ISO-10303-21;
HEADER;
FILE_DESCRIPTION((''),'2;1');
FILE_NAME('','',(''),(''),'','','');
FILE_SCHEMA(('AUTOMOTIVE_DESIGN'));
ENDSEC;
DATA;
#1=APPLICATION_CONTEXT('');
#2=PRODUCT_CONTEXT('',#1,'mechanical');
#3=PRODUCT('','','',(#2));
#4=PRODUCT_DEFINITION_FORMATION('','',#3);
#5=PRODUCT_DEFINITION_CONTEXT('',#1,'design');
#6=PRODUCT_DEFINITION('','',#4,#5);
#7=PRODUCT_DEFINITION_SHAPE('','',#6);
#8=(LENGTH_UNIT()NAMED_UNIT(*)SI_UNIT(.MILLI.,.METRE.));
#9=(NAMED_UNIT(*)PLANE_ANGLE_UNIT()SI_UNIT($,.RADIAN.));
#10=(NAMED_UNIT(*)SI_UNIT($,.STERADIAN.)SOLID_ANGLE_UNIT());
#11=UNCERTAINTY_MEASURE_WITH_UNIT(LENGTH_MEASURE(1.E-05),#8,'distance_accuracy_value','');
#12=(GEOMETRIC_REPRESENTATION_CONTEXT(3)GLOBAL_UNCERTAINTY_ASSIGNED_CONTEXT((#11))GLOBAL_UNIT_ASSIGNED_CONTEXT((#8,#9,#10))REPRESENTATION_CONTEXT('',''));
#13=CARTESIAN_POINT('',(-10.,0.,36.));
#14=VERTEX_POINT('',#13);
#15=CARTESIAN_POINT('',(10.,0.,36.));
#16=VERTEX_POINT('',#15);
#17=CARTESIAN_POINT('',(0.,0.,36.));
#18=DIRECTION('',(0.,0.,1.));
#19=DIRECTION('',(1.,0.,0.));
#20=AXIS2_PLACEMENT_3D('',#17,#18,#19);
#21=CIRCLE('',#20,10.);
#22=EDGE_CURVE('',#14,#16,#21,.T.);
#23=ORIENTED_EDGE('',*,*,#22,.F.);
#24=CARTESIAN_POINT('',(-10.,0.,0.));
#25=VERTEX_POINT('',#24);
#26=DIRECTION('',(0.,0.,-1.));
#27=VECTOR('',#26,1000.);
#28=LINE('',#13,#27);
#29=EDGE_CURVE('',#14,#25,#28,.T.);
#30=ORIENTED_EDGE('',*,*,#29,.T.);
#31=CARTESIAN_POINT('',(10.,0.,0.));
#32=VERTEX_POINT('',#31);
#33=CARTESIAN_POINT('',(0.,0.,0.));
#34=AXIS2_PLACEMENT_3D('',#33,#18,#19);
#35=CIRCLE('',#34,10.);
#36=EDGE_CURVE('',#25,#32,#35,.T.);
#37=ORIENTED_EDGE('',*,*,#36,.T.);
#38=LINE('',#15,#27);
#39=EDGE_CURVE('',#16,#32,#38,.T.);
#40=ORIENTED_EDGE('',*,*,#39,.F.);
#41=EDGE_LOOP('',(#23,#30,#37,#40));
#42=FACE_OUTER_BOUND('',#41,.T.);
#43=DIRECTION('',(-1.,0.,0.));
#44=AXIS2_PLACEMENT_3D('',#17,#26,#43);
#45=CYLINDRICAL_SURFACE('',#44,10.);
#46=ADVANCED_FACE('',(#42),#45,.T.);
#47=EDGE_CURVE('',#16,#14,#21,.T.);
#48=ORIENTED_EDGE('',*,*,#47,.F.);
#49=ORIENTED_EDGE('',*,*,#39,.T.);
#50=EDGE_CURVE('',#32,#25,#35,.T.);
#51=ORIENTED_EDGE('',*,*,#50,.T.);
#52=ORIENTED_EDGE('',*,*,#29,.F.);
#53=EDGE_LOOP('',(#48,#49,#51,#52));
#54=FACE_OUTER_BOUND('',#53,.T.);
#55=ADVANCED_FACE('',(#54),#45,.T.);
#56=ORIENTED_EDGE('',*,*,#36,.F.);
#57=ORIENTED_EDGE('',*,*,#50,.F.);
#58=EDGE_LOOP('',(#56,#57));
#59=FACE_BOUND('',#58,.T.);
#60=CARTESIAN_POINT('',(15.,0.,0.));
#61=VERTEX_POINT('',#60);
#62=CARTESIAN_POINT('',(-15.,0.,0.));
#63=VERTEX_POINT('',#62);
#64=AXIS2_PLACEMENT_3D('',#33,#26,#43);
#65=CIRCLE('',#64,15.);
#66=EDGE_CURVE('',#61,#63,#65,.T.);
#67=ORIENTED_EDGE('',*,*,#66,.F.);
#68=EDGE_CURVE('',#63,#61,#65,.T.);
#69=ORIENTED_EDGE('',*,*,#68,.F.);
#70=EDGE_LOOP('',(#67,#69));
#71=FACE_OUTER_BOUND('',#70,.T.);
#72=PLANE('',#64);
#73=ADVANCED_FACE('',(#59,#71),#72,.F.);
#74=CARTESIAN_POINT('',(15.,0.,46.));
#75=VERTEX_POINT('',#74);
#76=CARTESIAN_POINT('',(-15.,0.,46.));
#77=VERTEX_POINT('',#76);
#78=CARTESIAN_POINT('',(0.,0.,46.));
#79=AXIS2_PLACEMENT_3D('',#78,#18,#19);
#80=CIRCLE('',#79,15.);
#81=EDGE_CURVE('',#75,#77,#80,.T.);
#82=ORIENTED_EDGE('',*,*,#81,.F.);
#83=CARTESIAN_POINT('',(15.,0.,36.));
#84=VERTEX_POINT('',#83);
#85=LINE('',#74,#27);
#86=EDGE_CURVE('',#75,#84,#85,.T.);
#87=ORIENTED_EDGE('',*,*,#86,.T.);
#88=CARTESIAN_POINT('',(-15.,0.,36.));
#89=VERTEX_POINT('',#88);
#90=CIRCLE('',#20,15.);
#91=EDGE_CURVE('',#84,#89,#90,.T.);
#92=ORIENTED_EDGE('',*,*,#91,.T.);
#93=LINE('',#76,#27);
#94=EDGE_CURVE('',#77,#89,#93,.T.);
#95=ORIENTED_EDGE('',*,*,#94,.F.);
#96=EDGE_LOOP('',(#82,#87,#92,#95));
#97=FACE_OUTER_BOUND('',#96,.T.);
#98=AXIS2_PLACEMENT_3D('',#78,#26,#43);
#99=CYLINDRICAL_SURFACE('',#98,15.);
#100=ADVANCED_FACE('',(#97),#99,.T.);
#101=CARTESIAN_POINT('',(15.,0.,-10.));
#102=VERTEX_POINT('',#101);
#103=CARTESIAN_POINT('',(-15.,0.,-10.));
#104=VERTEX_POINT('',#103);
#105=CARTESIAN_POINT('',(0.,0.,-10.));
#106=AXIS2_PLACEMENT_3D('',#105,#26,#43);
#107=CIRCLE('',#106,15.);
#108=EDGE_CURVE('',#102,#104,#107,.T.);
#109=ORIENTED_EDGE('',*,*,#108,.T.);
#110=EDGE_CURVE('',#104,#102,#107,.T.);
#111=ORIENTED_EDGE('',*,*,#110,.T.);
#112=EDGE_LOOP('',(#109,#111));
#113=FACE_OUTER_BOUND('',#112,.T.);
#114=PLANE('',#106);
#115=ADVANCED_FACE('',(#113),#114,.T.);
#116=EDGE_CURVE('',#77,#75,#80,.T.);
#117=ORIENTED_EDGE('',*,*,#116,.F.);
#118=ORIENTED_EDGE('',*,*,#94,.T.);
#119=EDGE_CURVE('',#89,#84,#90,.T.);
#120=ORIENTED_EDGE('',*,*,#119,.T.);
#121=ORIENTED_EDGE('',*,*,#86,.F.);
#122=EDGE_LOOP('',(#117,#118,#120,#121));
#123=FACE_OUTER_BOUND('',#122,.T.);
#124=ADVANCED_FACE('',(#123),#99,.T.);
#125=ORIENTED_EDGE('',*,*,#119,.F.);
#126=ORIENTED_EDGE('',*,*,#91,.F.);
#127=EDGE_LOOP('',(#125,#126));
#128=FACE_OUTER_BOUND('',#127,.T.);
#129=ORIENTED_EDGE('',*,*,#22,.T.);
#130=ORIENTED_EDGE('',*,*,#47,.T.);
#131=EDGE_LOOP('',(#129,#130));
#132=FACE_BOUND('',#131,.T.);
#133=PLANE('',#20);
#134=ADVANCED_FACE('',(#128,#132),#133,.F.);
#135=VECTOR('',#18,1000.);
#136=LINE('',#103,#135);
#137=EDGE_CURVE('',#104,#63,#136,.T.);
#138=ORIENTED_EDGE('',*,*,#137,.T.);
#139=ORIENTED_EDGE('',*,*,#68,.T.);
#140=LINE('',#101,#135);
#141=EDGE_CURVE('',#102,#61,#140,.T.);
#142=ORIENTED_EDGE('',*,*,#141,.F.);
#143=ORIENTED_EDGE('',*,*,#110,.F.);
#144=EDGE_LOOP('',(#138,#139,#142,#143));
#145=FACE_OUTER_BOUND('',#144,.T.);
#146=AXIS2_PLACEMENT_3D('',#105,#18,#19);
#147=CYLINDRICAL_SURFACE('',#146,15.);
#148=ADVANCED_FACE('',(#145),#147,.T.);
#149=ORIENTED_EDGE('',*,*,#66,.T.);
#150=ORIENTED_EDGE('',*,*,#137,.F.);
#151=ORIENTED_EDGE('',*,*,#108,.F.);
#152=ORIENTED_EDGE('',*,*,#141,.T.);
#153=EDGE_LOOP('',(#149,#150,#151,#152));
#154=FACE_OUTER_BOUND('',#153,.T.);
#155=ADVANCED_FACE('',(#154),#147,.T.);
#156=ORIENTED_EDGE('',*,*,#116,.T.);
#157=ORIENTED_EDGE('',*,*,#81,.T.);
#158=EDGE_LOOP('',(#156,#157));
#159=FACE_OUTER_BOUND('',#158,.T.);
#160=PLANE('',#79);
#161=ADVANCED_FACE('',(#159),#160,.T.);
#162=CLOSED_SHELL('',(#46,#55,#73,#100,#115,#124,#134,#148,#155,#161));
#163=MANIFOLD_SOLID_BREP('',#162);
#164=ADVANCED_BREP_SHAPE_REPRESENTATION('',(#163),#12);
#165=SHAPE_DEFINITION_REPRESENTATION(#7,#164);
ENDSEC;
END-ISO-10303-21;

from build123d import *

# Parameters (mm, degrees)
SKETCH1_R           = 10
BOSS_EXTRUDE1_DEPTH = 36
SKETCH2_R           = 15
BOSS_EXTRUDE2_DEPTH = 10
BOSS_EXTRUDE3_START = 10
SKETCH3_R           = 15
BOSS_EXTRUDE3_DEPTH = 10


with BuildPart() as part:
    # Sketch1 → Boss-Extrude1 (new body)
    with BuildSketch(Plane.XY):
        Circle(SKETCH1_R)
    extrude(amount=BOSS_EXTRUDE1_DEPTH)

    # Sketch2 → Boss-Extrude2 (add)
    with BuildSketch(Plane.XY.offset(36)):
        Circle(SKETCH2_R)
    extrude(amount=BOSS_EXTRUDE2_DEPTH)

    # Sketch3 → Boss-Extrude3 (add)
    with BuildSketch(Plane(origin=(0, 0, 0), x_dir=(-1, 0, 0), z_dir=(0, 0, -1)).offset(BOSS_EXTRUDE3_START)):
        with Locations(Location((0, 0, 0), (0, 0, 180))):
            Circle(SKETCH3_R)
    extrude(amount=-BOSS_EXTRUDE3_DEPTH)


solid = part.part
